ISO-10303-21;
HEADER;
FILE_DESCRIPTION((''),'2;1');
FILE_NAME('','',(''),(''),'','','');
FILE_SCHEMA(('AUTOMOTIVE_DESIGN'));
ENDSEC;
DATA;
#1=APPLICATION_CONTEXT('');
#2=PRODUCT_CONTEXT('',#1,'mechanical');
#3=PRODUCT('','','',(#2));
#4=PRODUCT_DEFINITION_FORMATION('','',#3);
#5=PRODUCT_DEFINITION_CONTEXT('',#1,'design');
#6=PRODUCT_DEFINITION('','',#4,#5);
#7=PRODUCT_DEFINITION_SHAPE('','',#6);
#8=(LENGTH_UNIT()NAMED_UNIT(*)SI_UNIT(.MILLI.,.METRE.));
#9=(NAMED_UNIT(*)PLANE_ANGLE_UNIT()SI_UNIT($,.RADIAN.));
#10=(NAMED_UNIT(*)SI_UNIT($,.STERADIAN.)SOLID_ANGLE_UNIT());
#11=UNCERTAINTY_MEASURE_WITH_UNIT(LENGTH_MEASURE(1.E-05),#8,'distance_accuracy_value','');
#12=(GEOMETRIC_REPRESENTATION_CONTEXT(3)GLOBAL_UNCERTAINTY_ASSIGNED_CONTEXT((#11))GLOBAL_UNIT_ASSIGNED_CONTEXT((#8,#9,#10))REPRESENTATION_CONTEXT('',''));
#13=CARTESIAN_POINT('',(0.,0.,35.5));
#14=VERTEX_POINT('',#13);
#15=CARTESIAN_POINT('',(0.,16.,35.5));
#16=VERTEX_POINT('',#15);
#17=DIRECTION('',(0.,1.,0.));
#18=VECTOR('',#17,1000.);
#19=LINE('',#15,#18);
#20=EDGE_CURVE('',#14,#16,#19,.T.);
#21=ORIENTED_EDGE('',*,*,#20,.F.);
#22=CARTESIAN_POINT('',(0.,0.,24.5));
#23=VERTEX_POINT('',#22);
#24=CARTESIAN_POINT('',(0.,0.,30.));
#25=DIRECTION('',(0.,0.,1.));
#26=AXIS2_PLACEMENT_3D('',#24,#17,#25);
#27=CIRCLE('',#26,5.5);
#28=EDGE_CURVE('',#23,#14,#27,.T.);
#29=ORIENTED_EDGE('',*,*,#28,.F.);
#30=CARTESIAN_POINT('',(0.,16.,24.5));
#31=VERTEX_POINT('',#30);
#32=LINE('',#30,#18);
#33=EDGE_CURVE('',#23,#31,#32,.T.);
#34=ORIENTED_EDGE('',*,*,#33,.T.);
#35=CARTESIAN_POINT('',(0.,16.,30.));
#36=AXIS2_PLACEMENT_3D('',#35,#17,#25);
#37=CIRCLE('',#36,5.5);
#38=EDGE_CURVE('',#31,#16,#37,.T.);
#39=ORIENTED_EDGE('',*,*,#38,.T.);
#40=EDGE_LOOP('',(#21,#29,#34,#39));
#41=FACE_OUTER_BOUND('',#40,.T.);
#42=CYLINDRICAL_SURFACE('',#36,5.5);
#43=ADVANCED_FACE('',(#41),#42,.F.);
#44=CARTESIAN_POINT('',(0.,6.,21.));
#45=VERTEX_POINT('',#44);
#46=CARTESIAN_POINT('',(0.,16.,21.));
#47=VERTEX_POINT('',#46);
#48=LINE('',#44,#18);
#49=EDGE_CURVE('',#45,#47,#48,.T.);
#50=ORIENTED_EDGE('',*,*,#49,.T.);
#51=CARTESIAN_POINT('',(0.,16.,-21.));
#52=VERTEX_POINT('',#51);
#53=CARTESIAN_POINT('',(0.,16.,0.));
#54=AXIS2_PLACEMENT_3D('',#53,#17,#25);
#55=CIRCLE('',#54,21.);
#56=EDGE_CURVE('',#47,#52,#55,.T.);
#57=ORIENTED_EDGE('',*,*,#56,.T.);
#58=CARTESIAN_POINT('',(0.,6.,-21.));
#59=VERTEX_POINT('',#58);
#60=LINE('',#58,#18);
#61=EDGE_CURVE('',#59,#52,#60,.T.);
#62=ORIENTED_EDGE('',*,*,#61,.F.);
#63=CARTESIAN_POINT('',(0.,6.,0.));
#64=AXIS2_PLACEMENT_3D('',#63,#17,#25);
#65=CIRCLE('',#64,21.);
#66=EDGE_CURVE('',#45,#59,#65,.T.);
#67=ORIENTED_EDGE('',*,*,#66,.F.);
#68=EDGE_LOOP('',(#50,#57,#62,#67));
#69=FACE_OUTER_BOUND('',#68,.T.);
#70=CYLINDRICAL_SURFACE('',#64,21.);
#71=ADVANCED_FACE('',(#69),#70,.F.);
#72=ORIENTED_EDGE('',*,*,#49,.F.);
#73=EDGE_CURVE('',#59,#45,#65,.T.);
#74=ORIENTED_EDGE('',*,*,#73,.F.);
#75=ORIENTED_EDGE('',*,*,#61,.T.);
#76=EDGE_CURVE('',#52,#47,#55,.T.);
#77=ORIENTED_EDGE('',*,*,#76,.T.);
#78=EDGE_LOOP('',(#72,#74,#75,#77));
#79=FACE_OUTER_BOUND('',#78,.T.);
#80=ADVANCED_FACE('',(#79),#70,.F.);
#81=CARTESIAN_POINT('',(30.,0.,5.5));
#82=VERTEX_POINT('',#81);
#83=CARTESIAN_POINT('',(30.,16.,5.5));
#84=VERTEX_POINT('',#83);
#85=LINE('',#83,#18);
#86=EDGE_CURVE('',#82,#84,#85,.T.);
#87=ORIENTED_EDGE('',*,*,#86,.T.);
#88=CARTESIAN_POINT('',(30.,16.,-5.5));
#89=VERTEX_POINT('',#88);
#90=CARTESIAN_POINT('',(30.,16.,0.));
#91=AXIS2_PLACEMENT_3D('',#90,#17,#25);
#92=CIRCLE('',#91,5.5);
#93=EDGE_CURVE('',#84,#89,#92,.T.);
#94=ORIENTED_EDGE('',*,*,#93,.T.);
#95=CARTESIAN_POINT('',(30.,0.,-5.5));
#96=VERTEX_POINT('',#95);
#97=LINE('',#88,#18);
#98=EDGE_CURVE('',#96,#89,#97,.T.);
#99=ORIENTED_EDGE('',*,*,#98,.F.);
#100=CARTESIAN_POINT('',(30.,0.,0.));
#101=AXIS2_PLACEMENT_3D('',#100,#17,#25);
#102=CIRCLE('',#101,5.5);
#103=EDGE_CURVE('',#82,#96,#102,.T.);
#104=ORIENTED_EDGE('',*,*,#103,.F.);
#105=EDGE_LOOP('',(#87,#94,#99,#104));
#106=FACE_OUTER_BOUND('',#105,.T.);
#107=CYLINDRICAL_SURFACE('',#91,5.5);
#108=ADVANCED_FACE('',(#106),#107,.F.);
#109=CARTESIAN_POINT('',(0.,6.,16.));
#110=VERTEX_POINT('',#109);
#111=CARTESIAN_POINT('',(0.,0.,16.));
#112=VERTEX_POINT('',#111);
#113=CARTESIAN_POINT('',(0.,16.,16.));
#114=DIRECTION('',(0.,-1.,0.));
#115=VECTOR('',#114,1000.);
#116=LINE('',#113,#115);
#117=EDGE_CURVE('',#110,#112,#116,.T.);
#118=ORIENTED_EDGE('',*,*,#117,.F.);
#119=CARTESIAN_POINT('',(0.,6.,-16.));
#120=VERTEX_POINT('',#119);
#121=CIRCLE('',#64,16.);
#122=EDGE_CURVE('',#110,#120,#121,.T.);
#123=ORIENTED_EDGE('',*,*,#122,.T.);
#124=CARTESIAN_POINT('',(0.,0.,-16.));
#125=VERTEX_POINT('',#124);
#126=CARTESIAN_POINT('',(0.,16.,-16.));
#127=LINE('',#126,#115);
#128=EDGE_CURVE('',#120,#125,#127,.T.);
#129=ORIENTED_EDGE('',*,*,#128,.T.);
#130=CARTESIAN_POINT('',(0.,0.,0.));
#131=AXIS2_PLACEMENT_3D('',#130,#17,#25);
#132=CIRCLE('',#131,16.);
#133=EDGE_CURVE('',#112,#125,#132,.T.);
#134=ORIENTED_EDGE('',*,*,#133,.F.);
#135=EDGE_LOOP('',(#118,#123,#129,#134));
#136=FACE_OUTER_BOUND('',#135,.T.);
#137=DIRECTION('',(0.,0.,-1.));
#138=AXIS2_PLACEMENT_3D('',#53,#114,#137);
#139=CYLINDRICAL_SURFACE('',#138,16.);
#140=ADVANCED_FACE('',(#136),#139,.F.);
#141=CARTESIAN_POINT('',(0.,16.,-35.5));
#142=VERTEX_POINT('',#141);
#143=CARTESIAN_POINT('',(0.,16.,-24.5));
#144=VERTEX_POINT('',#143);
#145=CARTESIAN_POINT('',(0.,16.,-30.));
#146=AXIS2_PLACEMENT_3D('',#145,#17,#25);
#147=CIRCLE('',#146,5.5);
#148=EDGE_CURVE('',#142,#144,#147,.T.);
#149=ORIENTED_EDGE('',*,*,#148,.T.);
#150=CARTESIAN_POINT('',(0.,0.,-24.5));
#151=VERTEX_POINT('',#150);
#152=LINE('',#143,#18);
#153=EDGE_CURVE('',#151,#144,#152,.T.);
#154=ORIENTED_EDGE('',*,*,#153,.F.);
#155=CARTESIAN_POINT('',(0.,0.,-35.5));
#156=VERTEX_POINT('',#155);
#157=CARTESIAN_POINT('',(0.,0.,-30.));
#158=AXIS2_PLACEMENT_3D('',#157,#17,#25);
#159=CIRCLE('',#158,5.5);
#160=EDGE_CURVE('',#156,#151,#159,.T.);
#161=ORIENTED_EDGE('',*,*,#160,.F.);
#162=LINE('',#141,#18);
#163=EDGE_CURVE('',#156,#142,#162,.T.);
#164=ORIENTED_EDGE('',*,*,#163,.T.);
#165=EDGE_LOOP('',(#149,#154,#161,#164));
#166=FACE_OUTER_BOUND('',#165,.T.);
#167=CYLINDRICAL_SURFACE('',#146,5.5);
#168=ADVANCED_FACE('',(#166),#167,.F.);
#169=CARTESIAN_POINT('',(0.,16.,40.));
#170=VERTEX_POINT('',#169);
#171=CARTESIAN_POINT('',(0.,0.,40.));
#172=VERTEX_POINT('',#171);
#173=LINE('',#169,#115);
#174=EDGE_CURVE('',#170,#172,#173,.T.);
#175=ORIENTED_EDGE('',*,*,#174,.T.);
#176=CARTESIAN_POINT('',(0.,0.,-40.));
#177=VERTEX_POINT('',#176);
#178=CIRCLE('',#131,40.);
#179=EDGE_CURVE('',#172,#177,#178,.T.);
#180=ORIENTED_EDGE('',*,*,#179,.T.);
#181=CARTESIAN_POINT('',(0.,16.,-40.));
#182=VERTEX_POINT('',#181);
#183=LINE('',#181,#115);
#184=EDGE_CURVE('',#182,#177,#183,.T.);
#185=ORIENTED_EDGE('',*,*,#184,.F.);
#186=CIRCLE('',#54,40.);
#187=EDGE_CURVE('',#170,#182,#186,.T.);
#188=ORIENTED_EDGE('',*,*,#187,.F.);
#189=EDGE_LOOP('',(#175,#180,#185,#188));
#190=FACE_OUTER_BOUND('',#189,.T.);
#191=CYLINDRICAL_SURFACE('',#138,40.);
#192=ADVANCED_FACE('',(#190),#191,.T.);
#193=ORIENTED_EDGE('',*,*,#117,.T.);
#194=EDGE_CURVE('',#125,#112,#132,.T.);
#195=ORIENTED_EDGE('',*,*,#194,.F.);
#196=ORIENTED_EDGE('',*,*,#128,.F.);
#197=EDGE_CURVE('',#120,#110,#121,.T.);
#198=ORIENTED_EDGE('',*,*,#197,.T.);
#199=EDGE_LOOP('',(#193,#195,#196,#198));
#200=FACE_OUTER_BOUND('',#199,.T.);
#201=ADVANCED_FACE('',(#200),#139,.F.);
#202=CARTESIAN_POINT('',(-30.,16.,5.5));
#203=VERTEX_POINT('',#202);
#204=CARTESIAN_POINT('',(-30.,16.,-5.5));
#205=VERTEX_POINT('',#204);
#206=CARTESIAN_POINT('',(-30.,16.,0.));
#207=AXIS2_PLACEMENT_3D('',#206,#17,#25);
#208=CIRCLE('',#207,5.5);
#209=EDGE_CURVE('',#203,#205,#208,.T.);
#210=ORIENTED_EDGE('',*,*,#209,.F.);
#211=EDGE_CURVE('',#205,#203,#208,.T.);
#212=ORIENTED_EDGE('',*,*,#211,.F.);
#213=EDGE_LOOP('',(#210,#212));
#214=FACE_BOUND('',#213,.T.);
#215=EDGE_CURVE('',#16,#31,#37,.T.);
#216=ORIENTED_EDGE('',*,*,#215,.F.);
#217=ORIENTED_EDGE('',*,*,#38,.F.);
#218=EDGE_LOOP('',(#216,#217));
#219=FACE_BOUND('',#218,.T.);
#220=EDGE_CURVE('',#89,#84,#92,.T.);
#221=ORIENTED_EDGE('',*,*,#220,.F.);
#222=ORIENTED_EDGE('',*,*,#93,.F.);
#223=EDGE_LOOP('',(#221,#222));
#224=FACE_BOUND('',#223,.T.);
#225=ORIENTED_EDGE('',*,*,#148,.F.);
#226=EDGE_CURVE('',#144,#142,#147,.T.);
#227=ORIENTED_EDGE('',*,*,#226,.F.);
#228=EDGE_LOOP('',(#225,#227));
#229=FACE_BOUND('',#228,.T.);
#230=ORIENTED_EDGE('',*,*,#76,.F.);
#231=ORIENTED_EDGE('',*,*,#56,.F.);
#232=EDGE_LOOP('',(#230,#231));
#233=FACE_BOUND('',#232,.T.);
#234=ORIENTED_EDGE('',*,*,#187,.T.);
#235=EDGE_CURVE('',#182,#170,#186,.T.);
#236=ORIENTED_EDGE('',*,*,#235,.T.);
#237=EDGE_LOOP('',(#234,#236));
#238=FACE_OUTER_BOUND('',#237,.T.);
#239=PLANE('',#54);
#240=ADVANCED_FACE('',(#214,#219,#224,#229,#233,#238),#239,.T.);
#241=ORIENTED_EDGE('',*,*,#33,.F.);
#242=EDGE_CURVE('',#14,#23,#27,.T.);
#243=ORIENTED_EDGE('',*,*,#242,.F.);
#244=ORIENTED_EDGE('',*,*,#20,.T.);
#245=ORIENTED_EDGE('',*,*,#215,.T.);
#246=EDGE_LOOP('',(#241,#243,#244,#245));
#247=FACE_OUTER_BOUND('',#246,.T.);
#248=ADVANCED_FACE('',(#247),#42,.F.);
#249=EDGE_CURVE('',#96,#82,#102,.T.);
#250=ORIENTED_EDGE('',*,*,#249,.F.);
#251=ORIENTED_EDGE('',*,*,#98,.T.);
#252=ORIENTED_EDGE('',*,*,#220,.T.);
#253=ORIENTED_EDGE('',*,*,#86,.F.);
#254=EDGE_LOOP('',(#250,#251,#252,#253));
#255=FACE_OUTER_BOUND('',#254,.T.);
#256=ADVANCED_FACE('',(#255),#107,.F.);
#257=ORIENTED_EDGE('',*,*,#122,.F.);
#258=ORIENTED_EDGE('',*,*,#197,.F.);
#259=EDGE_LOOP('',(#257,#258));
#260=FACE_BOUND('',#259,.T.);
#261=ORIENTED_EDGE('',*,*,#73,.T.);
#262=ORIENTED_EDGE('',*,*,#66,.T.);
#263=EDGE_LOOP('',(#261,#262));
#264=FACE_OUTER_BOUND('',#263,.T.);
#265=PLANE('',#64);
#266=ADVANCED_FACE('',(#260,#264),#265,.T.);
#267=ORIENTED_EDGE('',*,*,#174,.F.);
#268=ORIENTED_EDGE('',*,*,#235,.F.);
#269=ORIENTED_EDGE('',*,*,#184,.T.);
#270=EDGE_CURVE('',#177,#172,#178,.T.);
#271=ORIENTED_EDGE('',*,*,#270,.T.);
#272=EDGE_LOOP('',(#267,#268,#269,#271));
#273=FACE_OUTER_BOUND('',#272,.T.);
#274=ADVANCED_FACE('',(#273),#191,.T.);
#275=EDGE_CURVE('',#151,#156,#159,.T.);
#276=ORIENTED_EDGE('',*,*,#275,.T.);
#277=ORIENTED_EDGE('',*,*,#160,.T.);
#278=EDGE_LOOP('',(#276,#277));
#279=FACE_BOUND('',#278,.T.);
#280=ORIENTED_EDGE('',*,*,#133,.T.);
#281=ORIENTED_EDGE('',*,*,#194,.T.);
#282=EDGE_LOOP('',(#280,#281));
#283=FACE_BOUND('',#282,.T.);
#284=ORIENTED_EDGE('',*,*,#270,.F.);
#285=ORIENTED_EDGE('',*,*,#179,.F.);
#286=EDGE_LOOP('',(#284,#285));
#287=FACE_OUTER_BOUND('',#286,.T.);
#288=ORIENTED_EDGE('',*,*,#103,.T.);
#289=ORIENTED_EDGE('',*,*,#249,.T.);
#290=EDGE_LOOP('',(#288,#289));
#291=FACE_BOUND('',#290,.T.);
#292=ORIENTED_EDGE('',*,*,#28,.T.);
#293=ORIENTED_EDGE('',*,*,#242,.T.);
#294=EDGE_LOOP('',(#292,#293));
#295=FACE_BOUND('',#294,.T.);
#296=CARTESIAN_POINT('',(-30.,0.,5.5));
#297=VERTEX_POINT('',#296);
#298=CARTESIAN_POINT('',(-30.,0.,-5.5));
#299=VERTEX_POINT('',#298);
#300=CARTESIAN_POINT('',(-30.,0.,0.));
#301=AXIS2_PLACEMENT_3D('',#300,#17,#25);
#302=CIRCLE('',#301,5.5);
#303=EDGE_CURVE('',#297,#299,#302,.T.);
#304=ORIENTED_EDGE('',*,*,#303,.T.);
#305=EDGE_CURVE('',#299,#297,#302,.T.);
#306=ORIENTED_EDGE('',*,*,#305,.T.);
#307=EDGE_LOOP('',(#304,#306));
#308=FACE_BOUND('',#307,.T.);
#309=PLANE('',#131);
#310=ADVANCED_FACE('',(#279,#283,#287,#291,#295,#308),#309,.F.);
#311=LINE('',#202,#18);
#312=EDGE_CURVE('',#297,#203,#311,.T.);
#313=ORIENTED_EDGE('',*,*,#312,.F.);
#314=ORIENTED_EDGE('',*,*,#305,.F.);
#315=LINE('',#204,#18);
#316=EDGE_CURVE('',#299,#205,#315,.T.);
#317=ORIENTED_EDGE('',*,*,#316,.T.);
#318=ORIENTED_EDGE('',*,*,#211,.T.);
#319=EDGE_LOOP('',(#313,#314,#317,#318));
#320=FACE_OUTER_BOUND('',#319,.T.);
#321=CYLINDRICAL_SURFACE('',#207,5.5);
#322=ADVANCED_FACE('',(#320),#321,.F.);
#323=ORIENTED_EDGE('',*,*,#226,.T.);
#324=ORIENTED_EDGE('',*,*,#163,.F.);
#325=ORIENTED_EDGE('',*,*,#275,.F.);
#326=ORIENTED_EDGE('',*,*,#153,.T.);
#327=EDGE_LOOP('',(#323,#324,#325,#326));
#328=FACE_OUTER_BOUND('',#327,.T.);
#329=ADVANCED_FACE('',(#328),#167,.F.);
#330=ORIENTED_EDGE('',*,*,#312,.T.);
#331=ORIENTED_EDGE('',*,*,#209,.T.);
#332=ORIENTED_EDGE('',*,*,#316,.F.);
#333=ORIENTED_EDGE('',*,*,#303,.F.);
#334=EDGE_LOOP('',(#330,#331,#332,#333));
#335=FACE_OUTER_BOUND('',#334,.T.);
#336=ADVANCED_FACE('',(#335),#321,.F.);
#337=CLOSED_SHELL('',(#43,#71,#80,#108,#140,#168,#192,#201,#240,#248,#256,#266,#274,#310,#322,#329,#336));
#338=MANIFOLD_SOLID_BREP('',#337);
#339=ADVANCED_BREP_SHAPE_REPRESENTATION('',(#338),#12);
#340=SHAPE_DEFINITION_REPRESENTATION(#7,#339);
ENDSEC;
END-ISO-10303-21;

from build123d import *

# Parameters (mm, degrees)
SKETCH1_R                 = 40
SKETCH1_R_2               = 16
BOSS_EXTRUDE1_DEPTH       = 16
SKETCH2_R                 = 21
CUT_EXTRUDE1_DEPTH        = 10
M10_CLEARANCE_HOLE1_D     = 11
M10_CLEARANCE_HOLE1_DEPTH = 29.25
M10_CLEARANCE_HOLE1_TIP   = 3.304733405


with BuildPart() as part:
    # Sketch1 → Boss-Extrude1 (new body)
    with BuildSketch(Plane(origin=(0, 0, 0), x_dir=(1, 0, 0), z_dir=(0, 1, 0))):
        with Locations(Location((0, 0, 0), (0, 0, 270))):
            Circle(SKETCH1_R)
        with Locations(Location((0, 0, 0), (0, 0, 270))):
            Circle(SKETCH1_R_2, mode=Mode.SUBTRACT)
    extrude(amount=BOSS_EXTRUDE1_DEPTH)

    # Sketch2 → Cut-Extrude1 (cut)
    with BuildSketch(Plane(origin=(0, 16, 0), x_dir=(1, 0, 0), z_dir=(0, 1, 0))):
        with Locations(Location((0, 0, 0), (0, 0, 270))):
            Circle(SKETCH2_R)
    extrude(amount=-CUT_EXTRUDE1_DEPTH, mode=Mode.SUBTRACT)

    # M10 Clearance Hole1
    with Locations(Plane(origin=(0, 16, 0), x_dir=(1, 0, 0), z_dir=(0, 1, 0))):
        with Locations((0, -30), (0, 30), (-30, 0), (30, 0)):
            Hole(M10_CLEARANCE_HOLE1_D / 2, depth=M10_CLEARANCE_HOLE1_DEPTH)
            with Locations((0, 0, -(M10_CLEARANCE_HOLE1_DEPTH + M10_CLEARANCE_HOLE1_TIP / 2))):  # 118° drill point
                Cone(0, M10_CLEARANCE_HOLE1_D / 2, M10_CLEARANCE_HOLE1_TIP, mode=Mode.SUBTRACT)


solid = part.part
